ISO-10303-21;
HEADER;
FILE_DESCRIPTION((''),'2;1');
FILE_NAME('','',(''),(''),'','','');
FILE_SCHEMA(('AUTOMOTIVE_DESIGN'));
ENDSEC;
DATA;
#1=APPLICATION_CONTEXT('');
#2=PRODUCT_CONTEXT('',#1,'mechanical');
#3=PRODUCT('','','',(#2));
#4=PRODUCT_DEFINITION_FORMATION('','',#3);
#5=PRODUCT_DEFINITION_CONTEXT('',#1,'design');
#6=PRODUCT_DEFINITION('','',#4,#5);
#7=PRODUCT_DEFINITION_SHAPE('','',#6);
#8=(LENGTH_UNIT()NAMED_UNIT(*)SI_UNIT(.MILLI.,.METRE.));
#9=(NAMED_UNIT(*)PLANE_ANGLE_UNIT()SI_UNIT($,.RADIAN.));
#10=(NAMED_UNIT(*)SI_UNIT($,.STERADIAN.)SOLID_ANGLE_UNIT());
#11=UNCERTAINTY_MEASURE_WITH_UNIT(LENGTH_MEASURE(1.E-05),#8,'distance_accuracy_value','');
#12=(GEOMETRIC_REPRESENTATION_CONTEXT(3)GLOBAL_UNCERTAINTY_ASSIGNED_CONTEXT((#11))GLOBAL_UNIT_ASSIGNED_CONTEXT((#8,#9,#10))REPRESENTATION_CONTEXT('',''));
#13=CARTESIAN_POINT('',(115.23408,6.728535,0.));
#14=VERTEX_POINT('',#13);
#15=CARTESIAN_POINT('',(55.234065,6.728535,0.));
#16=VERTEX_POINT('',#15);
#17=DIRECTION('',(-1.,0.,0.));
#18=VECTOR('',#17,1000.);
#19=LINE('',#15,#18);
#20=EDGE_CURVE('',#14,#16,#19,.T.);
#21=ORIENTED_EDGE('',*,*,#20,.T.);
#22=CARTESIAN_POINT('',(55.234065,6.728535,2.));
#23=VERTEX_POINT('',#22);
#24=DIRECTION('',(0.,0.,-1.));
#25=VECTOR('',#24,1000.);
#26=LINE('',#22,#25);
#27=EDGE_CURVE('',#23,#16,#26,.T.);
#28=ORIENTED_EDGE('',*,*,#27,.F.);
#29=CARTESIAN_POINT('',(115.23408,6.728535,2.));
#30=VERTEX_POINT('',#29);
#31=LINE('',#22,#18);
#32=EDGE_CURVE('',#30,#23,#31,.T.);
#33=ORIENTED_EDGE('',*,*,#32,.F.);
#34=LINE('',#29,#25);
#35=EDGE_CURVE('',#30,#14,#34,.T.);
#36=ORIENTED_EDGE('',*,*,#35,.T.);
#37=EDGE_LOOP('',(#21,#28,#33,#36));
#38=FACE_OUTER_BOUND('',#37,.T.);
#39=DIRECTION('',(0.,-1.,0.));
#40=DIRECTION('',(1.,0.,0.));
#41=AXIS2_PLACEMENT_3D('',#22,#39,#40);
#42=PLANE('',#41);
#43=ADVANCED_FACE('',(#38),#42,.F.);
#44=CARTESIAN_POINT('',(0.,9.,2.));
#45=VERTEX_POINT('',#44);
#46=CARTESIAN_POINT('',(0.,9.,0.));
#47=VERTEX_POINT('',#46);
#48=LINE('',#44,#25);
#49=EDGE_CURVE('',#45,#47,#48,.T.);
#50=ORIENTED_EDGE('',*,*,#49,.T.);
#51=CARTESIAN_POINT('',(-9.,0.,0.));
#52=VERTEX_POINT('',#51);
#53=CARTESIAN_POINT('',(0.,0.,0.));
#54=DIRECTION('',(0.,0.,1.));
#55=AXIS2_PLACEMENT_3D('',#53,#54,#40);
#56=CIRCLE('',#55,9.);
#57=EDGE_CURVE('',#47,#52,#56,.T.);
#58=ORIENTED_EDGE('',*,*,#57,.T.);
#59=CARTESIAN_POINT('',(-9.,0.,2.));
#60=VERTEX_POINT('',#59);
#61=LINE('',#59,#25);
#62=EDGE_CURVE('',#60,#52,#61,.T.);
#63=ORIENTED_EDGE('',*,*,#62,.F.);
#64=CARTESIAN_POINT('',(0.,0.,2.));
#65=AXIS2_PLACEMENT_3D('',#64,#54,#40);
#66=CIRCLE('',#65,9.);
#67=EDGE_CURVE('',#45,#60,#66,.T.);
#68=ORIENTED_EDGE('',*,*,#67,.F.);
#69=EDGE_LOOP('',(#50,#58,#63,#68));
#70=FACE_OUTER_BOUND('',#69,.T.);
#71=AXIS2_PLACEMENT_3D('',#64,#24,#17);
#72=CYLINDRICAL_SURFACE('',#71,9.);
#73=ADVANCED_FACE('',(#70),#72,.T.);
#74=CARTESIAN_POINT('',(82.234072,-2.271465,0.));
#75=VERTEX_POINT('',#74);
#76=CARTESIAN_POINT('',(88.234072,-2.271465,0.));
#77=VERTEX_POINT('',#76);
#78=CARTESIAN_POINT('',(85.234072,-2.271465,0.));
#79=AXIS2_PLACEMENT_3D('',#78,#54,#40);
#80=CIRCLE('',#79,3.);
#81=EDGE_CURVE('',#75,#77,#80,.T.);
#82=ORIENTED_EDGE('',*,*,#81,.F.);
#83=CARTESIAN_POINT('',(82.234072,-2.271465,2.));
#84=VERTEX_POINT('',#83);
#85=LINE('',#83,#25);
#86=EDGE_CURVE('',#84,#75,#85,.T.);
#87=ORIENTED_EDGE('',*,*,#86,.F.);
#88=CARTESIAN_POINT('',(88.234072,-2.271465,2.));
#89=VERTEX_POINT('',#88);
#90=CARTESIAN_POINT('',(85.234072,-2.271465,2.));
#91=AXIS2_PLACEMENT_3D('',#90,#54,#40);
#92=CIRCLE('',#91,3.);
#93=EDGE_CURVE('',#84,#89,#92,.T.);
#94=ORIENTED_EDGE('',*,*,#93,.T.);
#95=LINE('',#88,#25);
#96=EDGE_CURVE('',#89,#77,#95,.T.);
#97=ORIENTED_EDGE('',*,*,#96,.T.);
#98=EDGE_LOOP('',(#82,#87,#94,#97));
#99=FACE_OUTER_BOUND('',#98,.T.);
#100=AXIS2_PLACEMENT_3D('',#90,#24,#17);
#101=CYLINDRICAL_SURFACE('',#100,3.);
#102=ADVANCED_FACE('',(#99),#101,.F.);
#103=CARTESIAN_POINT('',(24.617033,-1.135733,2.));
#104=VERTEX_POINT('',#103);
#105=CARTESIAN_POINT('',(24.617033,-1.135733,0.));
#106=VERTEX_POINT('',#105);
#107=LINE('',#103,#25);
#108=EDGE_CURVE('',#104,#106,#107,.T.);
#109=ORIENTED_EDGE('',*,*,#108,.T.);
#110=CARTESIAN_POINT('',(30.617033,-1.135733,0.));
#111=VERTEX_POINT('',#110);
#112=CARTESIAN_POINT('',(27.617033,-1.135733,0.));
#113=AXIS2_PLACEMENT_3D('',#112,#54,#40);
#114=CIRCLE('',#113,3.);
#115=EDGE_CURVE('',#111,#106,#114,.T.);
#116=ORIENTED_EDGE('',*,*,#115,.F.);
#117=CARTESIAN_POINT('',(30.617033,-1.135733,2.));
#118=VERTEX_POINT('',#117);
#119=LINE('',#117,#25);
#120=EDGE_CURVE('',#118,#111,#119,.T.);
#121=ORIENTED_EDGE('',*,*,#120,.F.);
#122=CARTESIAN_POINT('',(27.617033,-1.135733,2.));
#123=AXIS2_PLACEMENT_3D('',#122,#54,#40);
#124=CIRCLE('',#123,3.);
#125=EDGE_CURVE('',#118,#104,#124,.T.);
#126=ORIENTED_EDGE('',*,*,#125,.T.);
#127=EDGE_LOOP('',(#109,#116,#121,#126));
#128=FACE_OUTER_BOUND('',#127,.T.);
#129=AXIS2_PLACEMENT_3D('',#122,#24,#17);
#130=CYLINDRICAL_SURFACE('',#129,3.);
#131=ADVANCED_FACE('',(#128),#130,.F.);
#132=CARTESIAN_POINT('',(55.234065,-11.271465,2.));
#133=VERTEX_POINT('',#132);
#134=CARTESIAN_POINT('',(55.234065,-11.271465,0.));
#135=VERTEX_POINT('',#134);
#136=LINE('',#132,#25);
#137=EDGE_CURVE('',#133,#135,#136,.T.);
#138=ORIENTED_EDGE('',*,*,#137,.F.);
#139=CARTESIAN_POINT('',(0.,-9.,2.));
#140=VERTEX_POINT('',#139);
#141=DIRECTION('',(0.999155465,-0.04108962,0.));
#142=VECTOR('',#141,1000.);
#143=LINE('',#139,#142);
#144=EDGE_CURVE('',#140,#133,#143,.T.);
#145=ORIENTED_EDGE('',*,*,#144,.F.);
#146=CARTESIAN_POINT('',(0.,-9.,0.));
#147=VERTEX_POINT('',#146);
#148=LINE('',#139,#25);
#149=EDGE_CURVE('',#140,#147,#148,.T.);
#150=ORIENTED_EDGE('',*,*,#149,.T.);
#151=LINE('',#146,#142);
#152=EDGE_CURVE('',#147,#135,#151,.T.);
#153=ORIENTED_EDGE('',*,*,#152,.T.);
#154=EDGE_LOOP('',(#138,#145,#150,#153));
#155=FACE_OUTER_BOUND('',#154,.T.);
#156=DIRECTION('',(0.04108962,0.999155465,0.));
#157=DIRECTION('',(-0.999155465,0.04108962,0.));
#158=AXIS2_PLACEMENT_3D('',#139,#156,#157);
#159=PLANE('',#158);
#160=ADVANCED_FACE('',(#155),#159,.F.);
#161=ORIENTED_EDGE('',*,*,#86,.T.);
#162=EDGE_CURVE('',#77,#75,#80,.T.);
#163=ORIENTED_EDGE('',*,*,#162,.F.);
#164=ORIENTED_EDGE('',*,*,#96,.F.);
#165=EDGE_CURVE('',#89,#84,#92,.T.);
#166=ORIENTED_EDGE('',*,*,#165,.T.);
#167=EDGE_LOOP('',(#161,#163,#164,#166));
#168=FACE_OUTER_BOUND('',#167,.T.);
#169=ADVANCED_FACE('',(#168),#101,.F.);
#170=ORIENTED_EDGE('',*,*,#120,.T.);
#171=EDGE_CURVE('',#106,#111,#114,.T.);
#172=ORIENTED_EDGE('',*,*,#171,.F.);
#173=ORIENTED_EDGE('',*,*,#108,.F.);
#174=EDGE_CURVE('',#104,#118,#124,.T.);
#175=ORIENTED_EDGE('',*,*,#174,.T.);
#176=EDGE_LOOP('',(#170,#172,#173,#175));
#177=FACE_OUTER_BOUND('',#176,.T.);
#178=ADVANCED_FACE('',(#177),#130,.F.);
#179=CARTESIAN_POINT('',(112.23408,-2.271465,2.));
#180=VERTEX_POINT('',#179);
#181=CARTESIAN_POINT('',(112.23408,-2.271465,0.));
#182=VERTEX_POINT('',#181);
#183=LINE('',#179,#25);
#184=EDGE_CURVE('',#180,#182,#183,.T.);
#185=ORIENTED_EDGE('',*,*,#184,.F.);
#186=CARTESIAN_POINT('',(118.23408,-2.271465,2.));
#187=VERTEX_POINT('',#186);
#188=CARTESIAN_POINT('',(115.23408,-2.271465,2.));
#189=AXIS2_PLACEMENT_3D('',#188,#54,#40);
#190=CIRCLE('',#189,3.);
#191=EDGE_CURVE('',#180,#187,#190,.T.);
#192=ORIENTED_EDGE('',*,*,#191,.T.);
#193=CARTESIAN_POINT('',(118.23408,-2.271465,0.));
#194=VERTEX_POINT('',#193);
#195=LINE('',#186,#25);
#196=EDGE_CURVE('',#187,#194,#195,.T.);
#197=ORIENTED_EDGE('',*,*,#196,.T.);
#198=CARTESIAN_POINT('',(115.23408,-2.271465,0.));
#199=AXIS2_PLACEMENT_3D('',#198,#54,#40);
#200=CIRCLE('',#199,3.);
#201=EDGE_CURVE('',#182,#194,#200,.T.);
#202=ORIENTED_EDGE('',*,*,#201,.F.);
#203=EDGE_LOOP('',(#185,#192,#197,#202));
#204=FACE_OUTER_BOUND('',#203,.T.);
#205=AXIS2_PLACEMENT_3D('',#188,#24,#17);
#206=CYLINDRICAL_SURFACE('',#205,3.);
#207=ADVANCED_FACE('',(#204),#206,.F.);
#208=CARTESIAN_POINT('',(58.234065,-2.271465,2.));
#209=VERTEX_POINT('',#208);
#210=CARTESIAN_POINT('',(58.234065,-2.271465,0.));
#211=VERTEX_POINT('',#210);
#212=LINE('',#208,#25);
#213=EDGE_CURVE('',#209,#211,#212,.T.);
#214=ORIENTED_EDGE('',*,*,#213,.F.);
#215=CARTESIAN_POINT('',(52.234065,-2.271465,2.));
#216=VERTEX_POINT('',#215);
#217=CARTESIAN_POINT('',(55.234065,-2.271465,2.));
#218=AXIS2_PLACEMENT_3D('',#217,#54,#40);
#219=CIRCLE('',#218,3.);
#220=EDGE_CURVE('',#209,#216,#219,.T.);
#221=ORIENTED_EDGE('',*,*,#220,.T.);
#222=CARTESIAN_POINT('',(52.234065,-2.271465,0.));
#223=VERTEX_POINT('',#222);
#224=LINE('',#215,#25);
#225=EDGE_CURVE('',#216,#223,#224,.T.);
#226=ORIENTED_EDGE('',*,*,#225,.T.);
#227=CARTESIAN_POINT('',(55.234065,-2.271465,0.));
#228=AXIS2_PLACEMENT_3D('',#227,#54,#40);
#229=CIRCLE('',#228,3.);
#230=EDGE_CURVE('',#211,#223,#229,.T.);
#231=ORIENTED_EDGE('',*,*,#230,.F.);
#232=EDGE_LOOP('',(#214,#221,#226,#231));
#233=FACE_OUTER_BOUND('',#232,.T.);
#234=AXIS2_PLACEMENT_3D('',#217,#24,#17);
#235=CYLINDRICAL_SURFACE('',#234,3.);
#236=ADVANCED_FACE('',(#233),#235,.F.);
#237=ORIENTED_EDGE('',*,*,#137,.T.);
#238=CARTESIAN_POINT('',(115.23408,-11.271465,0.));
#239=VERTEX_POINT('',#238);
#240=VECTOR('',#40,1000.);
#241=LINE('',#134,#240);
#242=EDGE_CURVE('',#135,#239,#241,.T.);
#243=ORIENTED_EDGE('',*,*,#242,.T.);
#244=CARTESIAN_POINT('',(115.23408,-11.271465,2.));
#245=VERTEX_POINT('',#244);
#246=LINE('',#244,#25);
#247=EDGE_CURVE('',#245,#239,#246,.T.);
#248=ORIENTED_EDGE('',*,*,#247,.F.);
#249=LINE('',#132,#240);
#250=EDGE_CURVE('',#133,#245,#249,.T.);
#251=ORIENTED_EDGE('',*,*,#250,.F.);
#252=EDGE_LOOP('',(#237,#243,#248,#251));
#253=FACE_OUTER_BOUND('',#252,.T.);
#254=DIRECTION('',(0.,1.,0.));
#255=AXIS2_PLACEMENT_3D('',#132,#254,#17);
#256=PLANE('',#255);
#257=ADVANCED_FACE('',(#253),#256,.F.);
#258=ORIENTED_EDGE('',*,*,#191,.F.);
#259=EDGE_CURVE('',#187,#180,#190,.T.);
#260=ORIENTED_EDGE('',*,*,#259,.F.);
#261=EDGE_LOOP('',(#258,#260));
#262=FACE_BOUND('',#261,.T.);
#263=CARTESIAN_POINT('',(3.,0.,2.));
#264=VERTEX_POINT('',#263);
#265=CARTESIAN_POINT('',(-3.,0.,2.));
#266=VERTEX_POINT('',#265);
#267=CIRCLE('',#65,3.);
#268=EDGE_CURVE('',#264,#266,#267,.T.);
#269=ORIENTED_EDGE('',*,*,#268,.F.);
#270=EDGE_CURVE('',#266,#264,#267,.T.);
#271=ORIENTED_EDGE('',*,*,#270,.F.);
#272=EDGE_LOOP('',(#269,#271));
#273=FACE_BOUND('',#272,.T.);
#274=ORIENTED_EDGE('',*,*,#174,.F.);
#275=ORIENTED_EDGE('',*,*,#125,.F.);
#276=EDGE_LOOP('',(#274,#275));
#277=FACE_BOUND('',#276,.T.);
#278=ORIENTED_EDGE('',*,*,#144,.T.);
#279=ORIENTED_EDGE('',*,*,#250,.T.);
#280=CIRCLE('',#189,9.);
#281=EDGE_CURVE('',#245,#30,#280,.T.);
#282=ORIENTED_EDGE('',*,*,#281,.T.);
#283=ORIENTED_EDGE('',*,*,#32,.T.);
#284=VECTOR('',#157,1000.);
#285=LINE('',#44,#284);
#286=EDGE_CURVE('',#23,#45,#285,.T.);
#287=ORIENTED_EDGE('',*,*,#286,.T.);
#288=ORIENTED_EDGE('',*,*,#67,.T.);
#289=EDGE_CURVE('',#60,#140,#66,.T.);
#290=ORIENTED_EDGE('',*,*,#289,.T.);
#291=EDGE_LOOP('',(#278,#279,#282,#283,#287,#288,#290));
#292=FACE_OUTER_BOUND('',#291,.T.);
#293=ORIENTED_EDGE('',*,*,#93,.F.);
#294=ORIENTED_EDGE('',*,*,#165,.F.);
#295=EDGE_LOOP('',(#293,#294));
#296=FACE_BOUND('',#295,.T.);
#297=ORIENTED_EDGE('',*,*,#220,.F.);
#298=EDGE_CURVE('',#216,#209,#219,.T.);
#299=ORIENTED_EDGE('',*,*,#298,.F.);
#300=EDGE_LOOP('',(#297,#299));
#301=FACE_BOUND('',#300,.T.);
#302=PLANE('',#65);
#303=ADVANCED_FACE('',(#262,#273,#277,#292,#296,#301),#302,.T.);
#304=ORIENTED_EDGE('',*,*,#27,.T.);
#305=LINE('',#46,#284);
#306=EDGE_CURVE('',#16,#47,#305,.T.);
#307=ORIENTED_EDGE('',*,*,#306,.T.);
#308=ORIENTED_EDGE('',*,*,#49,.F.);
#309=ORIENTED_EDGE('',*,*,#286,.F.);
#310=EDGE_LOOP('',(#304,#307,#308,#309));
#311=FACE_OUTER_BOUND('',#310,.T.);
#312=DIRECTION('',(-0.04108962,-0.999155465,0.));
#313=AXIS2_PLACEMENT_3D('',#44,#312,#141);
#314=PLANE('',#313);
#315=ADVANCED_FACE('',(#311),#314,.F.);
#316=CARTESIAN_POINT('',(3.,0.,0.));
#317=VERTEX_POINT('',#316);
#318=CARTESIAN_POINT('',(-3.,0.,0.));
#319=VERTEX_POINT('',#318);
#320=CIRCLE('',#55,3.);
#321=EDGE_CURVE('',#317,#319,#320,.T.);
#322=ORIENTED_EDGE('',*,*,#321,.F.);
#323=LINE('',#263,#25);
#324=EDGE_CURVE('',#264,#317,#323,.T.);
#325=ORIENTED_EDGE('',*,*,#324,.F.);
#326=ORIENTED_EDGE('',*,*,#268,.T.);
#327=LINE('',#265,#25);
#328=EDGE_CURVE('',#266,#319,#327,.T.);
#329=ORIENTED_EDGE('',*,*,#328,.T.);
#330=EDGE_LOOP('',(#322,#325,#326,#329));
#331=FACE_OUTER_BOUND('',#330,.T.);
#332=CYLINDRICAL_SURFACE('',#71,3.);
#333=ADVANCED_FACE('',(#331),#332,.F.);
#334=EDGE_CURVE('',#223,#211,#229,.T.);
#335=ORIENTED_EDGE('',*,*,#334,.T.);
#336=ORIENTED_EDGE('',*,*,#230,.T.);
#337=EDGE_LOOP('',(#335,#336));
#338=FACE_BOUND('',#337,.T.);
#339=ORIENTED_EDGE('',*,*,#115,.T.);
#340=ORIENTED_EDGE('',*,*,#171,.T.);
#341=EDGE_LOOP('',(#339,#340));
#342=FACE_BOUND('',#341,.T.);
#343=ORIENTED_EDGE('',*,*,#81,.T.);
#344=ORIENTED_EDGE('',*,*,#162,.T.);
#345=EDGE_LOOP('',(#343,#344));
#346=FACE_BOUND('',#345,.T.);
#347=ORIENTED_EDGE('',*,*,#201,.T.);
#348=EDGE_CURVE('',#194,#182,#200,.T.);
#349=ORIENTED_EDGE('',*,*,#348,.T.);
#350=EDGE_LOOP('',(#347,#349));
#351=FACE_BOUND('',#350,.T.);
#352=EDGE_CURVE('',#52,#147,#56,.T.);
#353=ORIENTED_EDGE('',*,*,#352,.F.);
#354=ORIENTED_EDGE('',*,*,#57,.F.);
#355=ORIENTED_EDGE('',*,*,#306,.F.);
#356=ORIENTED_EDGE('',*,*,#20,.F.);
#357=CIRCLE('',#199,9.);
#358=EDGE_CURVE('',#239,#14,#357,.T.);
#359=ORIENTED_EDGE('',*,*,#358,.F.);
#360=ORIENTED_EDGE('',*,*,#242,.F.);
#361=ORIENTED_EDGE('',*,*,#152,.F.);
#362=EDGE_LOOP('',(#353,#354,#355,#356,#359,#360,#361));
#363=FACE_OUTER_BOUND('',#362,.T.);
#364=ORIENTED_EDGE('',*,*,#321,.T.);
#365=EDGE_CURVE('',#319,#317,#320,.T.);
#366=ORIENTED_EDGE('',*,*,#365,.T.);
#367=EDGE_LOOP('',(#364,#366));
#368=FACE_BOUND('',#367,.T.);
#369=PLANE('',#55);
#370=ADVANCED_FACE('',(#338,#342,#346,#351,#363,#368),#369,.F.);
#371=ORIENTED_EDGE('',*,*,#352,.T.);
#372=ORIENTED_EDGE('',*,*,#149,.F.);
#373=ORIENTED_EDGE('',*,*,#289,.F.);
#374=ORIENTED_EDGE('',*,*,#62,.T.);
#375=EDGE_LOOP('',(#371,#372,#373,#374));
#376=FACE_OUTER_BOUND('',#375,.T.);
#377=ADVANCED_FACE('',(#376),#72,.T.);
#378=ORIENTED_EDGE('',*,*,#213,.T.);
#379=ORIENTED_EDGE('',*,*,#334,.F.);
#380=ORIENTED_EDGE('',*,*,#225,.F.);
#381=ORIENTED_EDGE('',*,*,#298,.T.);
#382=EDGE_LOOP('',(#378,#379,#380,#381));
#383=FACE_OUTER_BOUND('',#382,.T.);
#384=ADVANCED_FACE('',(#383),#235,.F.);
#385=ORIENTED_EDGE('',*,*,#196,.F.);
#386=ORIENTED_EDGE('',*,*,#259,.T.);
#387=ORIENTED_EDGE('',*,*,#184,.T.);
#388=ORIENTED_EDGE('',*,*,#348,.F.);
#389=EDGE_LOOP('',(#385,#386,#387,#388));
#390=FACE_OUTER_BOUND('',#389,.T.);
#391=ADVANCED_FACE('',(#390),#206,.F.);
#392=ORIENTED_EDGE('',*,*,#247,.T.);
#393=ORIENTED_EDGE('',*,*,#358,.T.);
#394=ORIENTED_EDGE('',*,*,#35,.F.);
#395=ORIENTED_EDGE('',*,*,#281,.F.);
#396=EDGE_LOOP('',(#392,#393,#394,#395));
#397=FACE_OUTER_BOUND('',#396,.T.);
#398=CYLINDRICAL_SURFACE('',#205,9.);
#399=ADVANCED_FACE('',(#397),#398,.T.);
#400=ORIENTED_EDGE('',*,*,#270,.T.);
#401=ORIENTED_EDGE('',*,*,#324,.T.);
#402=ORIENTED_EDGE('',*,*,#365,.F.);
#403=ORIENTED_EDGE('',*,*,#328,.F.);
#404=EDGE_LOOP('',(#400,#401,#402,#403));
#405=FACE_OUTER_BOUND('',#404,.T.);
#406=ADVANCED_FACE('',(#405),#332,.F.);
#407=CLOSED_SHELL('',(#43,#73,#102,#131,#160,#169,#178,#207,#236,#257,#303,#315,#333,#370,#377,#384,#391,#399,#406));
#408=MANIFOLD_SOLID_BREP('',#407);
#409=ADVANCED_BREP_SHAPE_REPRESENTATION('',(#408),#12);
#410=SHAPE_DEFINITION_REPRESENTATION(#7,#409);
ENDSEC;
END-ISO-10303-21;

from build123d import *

# Parameters (mm, degrees)
SKETCH1_R           = 3
BOSS_EXTRUDE1_DEPTH = 2


with BuildPart() as part:
    # Sketch1 → Boss-Extrude1 (new body)
    with BuildSketch(Plane.XY):
        with BuildLine():
            Line((0, 9), (55.234065112, 6.728534899))
            Line((55.234065112, 6.728534899), (115.234079808, 6.728534899))
            ThreePointArc((115.234079808, 6.728534899), (124.234079808, -2.271465101), (115.234079808, -11.271465101))
            Line((115.234079808, -11.271465101), (55.234065112, -11.271465101))
            Line((55.234065112, -11.271465101), (0, -9))
            ThreePointArc((0, -9), (-9, 0), (0, 9))
        make_face()
        Circle(SKETCH1_R, mode=Mode.SUBTRACT)
        with Locations((55.234065112, -2.271465101)):
            Circle(SKETCH1_R, mode=Mode.SUBTRACT)
        with Locations((115.234079808, -2.271465101)):
            Circle(SKETCH1_R, mode=Mode.SUBTRACT)
        with Locations((27.617032556, -1.13573255)):
            Circle(SKETCH1_R, mode=Mode.SUBTRACT)
        with Locations((85.23407246, -2.271465101)):
            Circle(SKETCH1_R, mode=Mode.SUBTRACT)
    extrude(amount=BOSS_EXTRUDE1_DEPTH)


solid = part.part
